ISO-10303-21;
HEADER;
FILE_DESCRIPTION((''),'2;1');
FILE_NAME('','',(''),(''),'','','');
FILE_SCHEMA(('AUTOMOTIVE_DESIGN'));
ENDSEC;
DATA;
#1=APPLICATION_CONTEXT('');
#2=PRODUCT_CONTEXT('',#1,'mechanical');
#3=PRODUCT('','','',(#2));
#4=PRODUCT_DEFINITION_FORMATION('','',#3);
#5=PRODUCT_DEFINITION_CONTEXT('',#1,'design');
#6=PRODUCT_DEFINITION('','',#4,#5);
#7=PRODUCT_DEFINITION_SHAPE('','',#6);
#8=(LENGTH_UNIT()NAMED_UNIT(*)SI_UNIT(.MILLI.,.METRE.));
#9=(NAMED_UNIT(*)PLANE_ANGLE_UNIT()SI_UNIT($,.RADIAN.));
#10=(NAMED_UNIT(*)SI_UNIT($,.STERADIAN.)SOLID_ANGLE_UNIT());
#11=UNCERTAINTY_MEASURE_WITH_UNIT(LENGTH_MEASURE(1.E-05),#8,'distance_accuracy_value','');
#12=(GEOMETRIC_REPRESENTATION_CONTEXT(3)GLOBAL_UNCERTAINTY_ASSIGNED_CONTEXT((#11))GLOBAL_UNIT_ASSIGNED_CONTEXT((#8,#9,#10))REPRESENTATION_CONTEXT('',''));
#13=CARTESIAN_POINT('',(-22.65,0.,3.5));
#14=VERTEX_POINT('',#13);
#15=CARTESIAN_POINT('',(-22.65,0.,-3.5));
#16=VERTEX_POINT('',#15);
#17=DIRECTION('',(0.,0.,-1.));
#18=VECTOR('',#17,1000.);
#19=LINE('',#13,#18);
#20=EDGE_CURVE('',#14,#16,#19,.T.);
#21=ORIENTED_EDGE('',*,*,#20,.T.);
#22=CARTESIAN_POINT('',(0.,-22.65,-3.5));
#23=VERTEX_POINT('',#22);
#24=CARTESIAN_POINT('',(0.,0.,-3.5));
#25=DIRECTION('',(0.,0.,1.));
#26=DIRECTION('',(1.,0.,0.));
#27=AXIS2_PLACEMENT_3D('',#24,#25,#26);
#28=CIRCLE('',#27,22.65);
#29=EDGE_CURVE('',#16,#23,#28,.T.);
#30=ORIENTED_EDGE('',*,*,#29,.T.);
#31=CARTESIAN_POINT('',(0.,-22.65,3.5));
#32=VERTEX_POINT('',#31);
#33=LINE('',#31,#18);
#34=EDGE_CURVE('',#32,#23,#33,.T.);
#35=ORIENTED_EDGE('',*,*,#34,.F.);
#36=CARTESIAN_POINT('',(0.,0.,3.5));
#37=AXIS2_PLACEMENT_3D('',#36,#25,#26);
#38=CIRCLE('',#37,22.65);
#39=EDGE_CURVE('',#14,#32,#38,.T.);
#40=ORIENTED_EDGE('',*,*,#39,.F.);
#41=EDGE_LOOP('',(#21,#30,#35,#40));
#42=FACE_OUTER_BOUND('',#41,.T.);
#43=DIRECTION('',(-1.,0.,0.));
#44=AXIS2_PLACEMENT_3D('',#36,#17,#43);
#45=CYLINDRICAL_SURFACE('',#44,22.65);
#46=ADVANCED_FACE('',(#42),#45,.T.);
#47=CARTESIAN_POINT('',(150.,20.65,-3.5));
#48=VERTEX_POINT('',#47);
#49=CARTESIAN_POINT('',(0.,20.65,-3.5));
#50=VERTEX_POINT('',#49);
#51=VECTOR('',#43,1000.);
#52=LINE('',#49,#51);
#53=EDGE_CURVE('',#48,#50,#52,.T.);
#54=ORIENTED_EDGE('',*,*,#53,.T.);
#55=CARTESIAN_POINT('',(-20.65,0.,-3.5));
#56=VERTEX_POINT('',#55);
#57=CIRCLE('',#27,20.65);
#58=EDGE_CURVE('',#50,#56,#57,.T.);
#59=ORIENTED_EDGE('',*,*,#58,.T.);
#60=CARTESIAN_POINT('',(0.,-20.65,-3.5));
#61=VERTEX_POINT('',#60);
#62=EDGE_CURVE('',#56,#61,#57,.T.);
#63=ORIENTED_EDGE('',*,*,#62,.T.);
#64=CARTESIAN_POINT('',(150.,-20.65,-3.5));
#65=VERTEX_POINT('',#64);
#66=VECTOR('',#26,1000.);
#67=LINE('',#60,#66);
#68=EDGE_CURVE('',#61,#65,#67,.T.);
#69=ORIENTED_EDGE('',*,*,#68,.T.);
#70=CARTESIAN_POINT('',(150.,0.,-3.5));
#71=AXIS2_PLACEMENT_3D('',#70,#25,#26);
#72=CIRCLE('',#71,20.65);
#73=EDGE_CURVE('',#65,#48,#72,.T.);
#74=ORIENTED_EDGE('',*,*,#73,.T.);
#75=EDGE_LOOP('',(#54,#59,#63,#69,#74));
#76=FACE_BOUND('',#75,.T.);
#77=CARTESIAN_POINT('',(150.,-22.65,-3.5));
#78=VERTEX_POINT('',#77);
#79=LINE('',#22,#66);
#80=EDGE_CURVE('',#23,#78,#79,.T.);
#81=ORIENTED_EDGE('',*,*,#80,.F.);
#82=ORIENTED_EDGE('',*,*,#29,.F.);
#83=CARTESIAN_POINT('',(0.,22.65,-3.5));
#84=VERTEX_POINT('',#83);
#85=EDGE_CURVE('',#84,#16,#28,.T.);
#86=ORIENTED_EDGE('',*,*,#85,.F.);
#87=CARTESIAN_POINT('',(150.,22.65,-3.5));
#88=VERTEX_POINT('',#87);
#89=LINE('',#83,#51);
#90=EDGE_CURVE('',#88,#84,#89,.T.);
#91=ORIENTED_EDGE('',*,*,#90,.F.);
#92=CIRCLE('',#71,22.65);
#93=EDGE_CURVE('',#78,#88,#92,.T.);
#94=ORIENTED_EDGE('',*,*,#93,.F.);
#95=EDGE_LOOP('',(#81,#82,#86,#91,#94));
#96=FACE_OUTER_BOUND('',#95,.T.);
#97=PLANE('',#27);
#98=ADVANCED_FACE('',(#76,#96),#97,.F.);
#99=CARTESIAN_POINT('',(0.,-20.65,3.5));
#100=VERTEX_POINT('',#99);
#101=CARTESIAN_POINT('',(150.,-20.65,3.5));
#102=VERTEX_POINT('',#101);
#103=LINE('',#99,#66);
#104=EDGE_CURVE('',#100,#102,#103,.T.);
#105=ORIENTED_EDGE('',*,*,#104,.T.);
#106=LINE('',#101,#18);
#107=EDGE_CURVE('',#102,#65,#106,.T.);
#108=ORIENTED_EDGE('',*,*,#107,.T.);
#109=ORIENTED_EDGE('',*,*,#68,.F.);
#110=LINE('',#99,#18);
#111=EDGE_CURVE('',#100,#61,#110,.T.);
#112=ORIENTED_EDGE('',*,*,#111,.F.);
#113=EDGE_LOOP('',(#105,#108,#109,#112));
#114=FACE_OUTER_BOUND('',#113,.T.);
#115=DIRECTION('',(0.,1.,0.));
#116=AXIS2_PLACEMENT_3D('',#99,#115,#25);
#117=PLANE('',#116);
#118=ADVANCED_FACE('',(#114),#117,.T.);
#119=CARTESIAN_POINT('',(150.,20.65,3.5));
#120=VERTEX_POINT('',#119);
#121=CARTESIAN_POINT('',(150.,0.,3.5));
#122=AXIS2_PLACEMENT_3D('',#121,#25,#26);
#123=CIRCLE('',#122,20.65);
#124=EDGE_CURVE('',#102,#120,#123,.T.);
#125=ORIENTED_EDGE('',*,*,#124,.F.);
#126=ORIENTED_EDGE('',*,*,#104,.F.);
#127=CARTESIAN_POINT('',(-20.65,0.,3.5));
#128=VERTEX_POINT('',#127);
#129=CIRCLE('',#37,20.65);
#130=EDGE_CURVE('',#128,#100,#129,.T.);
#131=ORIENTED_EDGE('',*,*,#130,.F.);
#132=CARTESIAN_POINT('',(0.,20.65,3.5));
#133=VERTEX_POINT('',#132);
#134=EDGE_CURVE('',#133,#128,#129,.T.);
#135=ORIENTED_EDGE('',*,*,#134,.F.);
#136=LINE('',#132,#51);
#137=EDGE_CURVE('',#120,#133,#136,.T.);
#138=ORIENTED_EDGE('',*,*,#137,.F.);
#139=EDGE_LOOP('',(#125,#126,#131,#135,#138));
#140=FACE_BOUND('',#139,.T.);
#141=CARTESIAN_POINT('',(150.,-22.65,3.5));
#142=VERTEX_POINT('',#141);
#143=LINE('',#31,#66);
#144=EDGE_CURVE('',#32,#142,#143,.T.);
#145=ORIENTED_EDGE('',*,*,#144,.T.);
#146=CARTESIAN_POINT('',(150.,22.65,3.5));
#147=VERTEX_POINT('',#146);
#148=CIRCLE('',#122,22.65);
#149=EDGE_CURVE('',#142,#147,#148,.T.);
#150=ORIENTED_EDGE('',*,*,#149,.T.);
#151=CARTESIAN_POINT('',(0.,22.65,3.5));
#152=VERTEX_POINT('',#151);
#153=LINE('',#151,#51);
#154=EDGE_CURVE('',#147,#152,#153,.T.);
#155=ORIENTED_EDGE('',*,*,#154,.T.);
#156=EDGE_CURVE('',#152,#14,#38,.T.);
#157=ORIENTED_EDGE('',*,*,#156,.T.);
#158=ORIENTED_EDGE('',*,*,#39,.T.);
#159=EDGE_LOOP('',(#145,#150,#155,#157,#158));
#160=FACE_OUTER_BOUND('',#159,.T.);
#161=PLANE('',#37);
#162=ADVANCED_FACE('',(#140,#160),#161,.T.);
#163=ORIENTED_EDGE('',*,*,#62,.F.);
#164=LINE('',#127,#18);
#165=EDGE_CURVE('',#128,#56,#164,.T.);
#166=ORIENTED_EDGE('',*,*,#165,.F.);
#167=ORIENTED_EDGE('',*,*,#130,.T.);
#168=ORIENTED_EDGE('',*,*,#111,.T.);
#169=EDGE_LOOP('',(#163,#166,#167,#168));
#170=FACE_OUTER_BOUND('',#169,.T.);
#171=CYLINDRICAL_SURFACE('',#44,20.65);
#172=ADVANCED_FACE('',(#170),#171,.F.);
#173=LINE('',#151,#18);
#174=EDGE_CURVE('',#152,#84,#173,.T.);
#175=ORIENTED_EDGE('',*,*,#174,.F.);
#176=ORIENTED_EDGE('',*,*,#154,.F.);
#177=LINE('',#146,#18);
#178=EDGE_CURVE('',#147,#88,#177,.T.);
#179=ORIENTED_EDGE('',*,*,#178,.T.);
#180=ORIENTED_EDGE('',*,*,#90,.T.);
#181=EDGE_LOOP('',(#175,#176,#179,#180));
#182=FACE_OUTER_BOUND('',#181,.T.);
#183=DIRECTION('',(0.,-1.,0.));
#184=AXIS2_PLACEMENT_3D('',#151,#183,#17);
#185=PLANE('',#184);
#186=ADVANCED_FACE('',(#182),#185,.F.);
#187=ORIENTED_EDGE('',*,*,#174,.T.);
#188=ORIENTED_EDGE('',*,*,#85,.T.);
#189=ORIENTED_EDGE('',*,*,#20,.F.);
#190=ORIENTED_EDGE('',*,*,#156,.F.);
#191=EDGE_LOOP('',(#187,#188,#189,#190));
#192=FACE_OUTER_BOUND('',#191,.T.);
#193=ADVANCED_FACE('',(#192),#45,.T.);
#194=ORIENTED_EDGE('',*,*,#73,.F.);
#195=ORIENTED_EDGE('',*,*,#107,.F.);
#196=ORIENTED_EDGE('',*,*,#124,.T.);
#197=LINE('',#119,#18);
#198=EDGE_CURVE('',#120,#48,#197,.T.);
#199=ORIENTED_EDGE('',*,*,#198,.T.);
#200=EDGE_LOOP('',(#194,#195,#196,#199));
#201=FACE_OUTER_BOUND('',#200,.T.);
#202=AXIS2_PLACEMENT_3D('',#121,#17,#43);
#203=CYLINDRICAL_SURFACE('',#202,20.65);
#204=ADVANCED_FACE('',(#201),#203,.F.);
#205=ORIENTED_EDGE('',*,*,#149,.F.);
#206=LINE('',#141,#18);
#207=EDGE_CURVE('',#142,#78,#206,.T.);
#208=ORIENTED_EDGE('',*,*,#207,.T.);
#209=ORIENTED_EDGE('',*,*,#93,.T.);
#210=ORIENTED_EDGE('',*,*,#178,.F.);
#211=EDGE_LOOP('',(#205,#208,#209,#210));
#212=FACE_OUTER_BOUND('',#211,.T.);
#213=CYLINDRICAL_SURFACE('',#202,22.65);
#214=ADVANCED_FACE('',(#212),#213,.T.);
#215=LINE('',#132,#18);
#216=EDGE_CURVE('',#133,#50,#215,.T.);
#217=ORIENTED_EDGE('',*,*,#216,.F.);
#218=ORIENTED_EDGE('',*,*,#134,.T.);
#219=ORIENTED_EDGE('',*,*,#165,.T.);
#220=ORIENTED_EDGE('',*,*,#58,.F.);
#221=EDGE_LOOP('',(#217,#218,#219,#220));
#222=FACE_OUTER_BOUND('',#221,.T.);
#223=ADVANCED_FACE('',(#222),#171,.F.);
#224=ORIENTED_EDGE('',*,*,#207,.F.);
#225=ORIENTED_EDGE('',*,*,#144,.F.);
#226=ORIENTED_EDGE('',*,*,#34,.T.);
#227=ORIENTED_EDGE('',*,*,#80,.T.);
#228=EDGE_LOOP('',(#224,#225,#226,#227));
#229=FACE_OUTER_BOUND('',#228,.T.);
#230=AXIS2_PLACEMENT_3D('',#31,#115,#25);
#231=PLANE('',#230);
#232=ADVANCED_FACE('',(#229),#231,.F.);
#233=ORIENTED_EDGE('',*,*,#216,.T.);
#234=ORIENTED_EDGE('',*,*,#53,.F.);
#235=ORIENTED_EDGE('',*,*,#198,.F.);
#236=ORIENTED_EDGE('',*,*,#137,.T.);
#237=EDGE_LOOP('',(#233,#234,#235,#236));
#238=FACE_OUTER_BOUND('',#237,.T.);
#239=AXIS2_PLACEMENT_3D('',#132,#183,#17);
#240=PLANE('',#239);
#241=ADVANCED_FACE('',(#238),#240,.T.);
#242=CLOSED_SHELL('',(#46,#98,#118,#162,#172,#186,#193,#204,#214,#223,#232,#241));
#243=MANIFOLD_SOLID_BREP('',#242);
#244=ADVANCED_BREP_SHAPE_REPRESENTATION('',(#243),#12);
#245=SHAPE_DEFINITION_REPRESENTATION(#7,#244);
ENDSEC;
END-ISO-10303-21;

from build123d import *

# Parameters (mm, degrees)
EXTRUDE_1_DEPTH = 3.5


with BuildPart() as part:
    # 草图1 → 拉伸-薄壁1 (new, symmetric)
    with BuildSketch(Plane.XY):
        with BuildLine():
            Line((150, -22.65), (0, -22.65))
            ThreePointArc((0, -22.65), (-22.65, 0), (0, 22.65))
            Line((0, 22.65), (150, 22.65))
            ThreePointArc((150, 22.65), (172.65, 0), (150, -22.65))
        make_face()
        with BuildLine():
            Line((150, -20.65), (0, -20.65))
            ThreePointArc((0, -20.65), (-20.65, 0), (0, 20.65))
            Line((0, 20.65), (150, 20.65))
            ThreePointArc((150, 20.65), (170.65, 0), (150, -20.65))
        make_face(mode=Mode.SUBTRACT)
    extrude(amount=EXTRUDE_1_DEPTH, both=True)


solid = part.part
